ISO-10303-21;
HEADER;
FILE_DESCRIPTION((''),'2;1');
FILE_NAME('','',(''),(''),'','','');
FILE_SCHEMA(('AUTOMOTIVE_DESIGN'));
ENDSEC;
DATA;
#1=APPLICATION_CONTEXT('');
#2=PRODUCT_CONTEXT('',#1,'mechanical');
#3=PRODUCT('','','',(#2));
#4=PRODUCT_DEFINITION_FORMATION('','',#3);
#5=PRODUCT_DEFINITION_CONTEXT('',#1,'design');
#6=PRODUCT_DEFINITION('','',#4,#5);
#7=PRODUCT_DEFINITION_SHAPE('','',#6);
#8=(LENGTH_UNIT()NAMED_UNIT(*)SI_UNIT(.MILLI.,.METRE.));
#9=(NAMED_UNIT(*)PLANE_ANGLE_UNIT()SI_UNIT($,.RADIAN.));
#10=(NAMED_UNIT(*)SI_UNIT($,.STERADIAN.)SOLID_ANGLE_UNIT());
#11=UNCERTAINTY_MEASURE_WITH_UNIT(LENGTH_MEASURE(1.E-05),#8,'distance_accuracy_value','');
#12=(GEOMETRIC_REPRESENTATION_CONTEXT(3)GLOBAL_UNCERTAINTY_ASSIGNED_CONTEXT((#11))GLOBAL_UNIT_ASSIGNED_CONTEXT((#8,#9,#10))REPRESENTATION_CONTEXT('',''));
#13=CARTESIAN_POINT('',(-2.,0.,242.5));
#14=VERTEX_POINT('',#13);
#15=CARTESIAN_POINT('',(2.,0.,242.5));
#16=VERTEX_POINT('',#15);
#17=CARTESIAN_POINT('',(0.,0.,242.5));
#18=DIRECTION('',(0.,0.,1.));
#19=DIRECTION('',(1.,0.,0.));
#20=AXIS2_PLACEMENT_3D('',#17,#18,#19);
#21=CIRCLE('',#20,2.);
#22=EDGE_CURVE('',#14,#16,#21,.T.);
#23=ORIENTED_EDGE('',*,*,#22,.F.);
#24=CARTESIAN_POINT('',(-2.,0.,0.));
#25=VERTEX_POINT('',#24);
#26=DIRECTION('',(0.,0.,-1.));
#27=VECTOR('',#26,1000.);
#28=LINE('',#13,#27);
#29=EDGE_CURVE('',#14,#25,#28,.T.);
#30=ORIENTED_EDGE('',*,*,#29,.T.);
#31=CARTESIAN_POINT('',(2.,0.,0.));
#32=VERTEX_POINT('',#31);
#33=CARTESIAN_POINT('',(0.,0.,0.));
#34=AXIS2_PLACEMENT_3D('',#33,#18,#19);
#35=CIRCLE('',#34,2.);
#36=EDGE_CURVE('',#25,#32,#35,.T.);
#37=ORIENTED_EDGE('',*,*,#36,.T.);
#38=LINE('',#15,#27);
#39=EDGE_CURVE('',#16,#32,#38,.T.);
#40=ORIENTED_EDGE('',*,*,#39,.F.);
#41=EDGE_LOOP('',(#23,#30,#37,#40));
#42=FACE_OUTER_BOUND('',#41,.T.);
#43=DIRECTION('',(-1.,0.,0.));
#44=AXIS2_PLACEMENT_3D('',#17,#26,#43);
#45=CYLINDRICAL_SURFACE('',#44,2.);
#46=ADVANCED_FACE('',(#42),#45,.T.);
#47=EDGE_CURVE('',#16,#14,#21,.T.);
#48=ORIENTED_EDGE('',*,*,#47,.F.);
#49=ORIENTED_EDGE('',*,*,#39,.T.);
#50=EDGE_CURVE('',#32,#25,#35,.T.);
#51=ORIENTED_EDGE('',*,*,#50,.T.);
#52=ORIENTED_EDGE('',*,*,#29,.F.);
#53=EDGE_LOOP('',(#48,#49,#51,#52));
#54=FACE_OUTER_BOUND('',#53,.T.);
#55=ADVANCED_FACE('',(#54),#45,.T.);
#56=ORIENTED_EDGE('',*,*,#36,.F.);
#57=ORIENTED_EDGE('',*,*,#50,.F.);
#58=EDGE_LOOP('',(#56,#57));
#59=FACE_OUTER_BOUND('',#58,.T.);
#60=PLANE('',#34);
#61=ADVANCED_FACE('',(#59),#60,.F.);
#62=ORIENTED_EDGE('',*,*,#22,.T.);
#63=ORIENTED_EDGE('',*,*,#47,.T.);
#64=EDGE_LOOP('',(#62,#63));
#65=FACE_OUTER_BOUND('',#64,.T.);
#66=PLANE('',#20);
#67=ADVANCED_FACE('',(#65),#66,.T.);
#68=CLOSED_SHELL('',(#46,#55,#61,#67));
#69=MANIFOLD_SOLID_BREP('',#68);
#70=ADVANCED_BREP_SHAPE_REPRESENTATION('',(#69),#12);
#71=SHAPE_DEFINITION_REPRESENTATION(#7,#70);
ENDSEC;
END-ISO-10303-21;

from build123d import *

# Parameters (mm, degrees)
SKETCH1_R           = 2
BOSS_EXTRUDE1_DEPTH = 242.5


with BuildPart() as part:
    # Sketch1 → Boss-Extrude1 (new body)
    with BuildSketch(Plane.XY):
        Circle(SKETCH1_R)
    extrude(amount=BOSS_EXTRUDE1_DEPTH)


solid = part.part
